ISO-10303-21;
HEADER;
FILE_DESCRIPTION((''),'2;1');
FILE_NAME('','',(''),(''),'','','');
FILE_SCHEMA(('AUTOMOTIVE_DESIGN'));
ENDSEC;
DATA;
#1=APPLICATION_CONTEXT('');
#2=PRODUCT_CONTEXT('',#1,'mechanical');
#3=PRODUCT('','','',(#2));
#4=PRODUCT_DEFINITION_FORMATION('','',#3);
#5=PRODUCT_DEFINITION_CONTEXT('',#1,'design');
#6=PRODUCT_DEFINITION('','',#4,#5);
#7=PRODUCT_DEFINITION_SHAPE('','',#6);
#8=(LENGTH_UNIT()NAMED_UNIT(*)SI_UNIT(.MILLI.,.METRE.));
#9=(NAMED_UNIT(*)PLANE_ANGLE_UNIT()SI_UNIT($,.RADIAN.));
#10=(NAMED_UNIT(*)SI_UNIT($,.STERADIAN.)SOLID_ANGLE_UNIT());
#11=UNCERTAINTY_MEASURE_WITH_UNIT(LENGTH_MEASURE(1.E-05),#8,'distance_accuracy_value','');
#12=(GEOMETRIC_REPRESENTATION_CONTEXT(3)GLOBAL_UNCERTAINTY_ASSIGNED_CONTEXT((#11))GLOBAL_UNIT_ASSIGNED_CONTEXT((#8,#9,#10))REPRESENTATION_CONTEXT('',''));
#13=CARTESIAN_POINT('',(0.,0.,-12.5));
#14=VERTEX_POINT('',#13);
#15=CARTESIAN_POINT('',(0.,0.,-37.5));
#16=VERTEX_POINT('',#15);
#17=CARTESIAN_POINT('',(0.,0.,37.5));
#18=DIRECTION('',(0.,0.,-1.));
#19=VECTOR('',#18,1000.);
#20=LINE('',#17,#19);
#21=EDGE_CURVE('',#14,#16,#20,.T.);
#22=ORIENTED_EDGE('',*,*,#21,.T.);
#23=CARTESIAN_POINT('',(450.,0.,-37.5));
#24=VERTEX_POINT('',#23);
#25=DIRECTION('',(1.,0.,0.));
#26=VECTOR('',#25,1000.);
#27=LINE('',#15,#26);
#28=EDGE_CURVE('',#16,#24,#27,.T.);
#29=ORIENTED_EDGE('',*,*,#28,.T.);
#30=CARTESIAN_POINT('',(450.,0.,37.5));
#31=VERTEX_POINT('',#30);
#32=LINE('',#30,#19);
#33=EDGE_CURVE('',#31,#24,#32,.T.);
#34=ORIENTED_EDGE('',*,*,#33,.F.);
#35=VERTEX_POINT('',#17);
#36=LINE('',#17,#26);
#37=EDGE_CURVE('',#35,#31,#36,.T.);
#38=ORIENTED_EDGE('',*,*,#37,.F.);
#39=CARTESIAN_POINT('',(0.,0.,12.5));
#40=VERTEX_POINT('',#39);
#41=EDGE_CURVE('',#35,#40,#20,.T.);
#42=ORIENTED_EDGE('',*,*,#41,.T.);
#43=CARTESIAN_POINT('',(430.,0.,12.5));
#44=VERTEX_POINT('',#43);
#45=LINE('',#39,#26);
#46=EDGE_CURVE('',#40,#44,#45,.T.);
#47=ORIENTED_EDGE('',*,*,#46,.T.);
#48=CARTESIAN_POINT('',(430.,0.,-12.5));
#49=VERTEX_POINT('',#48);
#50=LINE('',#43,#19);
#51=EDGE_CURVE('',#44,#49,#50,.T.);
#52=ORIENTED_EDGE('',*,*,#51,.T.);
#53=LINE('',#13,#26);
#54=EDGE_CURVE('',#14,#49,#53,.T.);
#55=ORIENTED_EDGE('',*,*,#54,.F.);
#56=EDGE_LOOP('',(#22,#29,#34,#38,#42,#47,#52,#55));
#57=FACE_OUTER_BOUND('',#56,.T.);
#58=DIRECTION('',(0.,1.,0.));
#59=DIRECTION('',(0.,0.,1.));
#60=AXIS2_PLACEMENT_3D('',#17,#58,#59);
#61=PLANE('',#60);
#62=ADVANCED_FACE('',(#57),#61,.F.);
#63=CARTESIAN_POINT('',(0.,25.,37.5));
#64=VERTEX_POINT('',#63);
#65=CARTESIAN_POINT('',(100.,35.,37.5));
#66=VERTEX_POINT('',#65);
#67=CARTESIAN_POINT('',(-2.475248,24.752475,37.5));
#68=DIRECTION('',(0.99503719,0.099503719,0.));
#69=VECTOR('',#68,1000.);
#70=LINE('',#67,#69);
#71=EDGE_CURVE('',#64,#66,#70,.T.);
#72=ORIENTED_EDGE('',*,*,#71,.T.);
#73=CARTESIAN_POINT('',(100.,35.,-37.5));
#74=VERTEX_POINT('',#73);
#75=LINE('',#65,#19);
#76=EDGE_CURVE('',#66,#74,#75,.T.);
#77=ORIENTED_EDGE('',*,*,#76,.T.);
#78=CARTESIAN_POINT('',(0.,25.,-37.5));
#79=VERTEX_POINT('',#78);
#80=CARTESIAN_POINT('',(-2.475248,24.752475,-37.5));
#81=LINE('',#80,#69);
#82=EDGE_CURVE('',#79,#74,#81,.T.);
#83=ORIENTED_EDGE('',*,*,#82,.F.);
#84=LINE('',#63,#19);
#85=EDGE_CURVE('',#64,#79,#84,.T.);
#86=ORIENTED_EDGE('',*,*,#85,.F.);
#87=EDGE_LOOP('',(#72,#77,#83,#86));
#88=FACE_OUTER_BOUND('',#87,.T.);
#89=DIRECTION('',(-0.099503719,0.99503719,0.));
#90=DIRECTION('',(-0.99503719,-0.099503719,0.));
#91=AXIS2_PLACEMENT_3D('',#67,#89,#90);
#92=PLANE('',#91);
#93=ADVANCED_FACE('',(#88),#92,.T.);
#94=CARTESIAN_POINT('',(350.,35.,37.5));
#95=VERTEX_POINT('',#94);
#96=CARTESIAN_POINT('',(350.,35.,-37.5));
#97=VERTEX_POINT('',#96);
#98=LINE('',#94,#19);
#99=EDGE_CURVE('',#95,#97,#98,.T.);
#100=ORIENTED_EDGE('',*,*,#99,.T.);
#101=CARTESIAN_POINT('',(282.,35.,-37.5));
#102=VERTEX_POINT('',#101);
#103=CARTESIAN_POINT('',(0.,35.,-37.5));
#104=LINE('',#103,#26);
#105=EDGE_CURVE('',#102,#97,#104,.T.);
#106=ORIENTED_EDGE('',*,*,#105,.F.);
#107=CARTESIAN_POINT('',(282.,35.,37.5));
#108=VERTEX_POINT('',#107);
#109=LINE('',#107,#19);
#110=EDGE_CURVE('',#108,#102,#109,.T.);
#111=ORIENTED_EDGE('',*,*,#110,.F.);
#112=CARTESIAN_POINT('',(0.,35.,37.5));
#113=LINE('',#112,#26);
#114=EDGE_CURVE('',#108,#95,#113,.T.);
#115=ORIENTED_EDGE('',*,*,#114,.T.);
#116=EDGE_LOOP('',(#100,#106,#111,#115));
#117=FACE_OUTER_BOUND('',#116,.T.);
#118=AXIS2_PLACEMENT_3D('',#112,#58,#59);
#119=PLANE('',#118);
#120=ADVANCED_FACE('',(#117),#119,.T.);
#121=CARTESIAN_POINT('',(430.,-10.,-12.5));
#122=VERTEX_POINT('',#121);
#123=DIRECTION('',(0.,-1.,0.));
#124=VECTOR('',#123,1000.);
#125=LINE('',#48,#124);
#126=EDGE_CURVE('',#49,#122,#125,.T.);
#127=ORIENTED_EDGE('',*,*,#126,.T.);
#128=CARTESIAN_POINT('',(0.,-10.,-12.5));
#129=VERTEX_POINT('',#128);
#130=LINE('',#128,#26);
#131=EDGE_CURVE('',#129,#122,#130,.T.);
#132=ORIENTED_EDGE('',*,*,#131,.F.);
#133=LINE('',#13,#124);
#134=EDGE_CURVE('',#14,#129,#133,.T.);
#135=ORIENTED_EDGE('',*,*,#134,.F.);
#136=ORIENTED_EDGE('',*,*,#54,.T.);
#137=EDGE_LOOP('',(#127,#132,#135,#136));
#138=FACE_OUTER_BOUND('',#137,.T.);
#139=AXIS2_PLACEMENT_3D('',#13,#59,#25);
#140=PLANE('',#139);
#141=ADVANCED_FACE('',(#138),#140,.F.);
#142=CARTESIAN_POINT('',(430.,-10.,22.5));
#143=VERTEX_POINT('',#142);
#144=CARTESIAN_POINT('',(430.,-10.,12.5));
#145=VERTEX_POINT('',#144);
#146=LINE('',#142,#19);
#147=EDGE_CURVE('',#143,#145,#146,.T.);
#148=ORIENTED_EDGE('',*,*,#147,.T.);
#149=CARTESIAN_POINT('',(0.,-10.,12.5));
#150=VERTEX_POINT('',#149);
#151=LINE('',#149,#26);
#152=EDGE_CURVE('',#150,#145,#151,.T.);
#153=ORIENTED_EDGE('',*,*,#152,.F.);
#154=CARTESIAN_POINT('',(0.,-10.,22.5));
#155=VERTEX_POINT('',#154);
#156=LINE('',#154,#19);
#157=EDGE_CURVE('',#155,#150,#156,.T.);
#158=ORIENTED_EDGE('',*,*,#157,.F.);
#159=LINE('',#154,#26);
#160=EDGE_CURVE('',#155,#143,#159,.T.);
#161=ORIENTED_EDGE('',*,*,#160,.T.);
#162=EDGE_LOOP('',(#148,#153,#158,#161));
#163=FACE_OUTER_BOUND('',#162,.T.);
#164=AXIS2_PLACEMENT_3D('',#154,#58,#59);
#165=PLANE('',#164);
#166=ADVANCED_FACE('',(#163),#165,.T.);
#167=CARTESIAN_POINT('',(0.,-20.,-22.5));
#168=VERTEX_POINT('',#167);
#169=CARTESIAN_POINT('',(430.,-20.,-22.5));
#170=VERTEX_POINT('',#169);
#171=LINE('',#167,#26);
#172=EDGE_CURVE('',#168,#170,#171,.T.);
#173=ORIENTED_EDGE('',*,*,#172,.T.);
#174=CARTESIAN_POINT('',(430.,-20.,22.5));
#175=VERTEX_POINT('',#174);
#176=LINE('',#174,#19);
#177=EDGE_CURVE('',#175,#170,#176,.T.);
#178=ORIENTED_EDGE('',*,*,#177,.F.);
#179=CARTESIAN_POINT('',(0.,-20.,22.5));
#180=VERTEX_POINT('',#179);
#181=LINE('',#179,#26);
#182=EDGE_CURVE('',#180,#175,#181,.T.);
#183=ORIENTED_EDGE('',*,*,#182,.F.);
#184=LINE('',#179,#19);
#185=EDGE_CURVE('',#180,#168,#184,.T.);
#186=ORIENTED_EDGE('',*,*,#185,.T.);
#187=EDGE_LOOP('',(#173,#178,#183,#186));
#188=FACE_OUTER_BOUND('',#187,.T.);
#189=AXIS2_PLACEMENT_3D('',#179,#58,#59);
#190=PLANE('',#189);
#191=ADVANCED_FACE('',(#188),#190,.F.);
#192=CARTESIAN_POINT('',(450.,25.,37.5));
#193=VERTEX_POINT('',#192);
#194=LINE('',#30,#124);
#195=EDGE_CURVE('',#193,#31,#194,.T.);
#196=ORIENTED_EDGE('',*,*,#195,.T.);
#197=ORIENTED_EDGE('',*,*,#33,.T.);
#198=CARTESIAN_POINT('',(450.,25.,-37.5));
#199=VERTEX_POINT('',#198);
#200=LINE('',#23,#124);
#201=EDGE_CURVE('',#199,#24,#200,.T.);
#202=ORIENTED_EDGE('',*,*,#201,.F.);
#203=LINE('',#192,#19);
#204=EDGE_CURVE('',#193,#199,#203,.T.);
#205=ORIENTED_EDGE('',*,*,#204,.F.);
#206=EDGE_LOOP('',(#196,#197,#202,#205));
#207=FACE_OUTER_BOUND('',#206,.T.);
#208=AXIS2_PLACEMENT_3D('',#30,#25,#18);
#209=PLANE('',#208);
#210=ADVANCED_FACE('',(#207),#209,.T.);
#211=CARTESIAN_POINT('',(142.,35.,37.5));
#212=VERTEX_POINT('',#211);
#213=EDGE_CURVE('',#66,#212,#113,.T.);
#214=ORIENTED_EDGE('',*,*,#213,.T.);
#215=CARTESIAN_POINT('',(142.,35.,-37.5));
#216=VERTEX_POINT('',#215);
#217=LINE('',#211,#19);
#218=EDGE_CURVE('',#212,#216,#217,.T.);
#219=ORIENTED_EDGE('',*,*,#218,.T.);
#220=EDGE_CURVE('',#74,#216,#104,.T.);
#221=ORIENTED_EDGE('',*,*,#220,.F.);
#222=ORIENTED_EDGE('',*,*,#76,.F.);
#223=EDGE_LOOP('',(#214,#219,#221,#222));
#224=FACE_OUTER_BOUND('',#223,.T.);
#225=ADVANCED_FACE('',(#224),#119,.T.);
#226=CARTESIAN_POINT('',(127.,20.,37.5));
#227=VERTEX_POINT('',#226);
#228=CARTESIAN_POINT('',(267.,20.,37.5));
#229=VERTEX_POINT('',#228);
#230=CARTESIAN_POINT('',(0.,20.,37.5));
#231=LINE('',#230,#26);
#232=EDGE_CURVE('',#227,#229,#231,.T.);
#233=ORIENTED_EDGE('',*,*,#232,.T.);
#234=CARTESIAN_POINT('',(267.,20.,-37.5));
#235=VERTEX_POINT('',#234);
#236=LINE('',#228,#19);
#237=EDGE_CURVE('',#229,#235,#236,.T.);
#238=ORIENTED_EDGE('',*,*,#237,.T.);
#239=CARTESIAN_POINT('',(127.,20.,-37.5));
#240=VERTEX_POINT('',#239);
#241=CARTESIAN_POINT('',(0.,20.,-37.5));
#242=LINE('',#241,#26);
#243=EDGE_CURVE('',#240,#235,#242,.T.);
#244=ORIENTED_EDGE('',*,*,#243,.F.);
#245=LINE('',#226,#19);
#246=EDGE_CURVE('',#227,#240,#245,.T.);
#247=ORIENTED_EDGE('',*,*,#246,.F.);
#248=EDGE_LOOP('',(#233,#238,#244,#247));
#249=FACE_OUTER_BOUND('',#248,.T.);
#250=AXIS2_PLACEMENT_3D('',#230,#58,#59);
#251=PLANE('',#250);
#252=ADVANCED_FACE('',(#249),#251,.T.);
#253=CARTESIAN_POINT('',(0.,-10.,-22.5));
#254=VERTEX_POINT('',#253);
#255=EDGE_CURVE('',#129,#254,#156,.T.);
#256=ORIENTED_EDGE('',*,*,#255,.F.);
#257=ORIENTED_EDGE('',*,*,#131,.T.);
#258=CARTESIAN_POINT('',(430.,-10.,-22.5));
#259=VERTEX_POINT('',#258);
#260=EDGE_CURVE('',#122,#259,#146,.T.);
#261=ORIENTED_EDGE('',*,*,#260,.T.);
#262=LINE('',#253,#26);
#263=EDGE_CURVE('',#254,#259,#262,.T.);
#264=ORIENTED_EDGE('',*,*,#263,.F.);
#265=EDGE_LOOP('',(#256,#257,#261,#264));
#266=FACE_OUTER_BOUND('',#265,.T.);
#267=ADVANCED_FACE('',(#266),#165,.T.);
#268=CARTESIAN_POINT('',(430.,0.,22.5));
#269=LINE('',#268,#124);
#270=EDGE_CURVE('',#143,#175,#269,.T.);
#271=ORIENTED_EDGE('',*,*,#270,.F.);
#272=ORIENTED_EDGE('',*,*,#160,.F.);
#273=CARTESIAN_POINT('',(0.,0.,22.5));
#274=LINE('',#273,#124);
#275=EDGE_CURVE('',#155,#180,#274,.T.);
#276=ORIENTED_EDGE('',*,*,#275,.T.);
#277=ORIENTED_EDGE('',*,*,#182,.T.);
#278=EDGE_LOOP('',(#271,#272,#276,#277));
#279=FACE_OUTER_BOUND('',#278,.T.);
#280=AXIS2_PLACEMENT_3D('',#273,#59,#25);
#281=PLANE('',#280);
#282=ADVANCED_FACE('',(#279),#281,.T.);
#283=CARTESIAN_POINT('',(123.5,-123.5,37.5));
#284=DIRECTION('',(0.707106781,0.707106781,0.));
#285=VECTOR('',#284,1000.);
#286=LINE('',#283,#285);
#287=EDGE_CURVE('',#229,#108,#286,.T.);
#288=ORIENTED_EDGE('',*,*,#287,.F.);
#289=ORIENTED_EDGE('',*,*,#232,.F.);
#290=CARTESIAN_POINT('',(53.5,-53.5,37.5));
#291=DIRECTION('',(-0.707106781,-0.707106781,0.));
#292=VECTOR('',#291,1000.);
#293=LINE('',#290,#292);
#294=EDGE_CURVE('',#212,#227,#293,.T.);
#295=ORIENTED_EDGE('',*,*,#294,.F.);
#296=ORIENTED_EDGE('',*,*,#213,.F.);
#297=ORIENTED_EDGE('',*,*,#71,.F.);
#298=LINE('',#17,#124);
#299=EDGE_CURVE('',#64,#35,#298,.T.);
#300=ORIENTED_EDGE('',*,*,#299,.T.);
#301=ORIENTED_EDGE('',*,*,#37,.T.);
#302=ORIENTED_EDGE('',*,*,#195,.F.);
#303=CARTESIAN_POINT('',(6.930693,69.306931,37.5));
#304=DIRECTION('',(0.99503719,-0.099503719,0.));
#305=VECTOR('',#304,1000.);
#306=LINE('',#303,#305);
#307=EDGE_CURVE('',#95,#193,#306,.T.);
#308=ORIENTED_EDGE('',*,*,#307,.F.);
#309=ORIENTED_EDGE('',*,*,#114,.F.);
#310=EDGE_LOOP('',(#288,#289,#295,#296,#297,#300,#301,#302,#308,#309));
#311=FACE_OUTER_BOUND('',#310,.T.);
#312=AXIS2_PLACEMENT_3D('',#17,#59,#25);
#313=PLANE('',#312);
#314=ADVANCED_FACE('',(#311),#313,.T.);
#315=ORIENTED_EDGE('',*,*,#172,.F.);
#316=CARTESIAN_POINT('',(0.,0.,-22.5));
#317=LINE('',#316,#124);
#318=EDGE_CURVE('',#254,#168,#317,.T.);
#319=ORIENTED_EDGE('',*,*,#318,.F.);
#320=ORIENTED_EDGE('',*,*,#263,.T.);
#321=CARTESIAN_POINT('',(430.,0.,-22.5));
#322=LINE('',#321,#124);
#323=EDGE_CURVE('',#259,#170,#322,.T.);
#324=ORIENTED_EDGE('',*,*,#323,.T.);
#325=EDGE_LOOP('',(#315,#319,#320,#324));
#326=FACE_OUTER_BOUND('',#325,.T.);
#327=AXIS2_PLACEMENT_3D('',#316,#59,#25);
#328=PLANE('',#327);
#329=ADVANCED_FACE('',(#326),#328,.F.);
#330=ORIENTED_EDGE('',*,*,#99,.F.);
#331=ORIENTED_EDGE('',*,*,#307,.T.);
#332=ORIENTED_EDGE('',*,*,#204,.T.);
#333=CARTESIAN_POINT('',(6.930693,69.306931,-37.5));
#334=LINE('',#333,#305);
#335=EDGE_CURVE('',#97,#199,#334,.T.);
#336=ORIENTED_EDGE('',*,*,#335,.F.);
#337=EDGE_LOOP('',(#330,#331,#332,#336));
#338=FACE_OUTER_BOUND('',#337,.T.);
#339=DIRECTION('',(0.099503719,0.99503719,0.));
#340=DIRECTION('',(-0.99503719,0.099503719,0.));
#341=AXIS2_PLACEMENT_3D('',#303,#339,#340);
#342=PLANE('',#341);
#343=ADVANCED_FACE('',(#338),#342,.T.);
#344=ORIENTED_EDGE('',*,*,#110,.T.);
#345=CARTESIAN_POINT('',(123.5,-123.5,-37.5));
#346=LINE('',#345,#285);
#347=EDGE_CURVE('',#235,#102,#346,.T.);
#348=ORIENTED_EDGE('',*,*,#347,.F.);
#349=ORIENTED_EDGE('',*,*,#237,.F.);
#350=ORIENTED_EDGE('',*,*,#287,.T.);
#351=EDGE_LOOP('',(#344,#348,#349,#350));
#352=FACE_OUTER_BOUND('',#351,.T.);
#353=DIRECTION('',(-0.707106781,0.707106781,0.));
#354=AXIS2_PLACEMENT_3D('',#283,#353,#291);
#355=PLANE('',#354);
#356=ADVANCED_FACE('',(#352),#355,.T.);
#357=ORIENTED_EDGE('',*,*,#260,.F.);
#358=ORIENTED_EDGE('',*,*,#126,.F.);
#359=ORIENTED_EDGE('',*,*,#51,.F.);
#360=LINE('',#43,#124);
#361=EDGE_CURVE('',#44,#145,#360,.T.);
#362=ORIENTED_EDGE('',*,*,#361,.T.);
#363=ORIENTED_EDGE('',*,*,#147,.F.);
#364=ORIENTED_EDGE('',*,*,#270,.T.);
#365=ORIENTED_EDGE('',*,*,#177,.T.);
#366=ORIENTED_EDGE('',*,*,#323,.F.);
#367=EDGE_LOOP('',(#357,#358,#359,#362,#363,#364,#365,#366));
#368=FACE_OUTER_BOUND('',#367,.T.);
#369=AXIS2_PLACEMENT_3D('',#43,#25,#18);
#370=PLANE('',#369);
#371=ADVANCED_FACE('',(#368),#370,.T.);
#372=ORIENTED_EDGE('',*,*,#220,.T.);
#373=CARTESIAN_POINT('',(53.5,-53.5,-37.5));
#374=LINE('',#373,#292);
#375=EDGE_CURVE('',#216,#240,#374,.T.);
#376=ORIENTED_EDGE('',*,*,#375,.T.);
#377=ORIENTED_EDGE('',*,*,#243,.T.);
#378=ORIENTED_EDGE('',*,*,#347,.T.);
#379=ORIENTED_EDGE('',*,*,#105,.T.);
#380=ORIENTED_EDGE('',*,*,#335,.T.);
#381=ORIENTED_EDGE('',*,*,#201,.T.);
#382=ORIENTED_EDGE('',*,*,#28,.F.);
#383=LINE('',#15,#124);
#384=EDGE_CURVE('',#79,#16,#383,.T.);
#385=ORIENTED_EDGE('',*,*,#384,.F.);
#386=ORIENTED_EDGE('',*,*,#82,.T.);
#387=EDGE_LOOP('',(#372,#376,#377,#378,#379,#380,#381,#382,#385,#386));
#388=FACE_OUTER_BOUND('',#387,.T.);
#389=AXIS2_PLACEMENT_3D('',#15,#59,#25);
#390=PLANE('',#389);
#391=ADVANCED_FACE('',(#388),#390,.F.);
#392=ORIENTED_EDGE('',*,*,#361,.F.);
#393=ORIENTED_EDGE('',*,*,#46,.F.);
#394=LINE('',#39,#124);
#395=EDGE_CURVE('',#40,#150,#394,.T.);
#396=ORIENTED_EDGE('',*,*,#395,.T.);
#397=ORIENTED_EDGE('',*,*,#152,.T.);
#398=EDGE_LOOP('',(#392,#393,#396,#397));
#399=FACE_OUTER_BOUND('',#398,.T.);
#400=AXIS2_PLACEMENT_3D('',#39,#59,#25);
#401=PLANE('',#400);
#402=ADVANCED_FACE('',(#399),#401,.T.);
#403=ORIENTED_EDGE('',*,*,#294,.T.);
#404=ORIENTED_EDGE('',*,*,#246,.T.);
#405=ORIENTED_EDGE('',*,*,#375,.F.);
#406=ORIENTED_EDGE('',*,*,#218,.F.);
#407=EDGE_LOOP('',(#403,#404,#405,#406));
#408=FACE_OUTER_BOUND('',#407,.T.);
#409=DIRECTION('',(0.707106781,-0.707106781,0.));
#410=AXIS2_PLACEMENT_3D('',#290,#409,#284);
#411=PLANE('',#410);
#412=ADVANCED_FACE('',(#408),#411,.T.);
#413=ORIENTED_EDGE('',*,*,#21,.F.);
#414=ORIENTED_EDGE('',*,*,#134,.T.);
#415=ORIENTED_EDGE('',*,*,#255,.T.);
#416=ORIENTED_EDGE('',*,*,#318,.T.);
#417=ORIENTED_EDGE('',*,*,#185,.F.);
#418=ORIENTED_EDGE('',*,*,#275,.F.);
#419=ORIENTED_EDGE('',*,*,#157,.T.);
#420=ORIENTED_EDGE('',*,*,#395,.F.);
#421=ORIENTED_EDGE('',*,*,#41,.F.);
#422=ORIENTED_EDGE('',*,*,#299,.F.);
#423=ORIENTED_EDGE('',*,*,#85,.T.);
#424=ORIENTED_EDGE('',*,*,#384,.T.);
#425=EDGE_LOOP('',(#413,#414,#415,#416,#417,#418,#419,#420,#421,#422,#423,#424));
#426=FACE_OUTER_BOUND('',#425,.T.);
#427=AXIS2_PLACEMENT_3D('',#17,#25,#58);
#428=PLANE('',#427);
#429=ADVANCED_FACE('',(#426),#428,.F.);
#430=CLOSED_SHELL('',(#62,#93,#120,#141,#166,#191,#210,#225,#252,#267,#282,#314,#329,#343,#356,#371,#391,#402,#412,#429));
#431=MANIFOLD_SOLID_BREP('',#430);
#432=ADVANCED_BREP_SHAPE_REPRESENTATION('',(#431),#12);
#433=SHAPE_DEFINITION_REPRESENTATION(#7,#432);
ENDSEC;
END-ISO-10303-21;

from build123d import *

# Parameters (mm, degrees)
BASE_BAR_EXTRUDE_75MM_DEPTH    = 37.5
SKETCH1_4_W                    = 430
SKETCH1_4_H                    = 10
PROFILE_REGION_BOSS_25MM_DEPTH = 12.5
SKETCH1_5_W                    = 430
SKETCH1_5_H                    = 10
PROFILE_REGION_BOSS_45MM_DEPTH = 22.5


with BuildPart() as part:
    # Bar Profile Sketch → Base Bar Extrude 75mm (new, symmetric)
    with BuildSketch(Plane.XY):
        Polygon((0, 25), (0, 0), (430, 0), (450, 0), (450, 25), (350, 35), (282, 35), (267, 20), (127, 20), (142, 35), (100, 35), align=None)
    extrude(amount=BASE_BAR_EXTRUDE_75MM_DEPTH, both=True)

    # Sketch1_4 → Profile Region Boss 25mm (add, symmetric)
    with BuildSketch(Plane.XY):
        with Locations((215, -5)):
            Rectangle(SKETCH1_4_W, SKETCH1_4_H)
    extrude(amount=PROFILE_REGION_BOSS_25MM_DEPTH, both=True)

    # Sketch1_5 → Profile Region Boss 45mm (add, symmetric)
    with BuildSketch(Plane.XY):
        with Locations((215, -15)):
            Rectangle(SKETCH1_5_W, SKETCH1_5_H)
    extrude(amount=PROFILE_REGION_BOSS_45MM_DEPTH, both=True)


solid = part.part
